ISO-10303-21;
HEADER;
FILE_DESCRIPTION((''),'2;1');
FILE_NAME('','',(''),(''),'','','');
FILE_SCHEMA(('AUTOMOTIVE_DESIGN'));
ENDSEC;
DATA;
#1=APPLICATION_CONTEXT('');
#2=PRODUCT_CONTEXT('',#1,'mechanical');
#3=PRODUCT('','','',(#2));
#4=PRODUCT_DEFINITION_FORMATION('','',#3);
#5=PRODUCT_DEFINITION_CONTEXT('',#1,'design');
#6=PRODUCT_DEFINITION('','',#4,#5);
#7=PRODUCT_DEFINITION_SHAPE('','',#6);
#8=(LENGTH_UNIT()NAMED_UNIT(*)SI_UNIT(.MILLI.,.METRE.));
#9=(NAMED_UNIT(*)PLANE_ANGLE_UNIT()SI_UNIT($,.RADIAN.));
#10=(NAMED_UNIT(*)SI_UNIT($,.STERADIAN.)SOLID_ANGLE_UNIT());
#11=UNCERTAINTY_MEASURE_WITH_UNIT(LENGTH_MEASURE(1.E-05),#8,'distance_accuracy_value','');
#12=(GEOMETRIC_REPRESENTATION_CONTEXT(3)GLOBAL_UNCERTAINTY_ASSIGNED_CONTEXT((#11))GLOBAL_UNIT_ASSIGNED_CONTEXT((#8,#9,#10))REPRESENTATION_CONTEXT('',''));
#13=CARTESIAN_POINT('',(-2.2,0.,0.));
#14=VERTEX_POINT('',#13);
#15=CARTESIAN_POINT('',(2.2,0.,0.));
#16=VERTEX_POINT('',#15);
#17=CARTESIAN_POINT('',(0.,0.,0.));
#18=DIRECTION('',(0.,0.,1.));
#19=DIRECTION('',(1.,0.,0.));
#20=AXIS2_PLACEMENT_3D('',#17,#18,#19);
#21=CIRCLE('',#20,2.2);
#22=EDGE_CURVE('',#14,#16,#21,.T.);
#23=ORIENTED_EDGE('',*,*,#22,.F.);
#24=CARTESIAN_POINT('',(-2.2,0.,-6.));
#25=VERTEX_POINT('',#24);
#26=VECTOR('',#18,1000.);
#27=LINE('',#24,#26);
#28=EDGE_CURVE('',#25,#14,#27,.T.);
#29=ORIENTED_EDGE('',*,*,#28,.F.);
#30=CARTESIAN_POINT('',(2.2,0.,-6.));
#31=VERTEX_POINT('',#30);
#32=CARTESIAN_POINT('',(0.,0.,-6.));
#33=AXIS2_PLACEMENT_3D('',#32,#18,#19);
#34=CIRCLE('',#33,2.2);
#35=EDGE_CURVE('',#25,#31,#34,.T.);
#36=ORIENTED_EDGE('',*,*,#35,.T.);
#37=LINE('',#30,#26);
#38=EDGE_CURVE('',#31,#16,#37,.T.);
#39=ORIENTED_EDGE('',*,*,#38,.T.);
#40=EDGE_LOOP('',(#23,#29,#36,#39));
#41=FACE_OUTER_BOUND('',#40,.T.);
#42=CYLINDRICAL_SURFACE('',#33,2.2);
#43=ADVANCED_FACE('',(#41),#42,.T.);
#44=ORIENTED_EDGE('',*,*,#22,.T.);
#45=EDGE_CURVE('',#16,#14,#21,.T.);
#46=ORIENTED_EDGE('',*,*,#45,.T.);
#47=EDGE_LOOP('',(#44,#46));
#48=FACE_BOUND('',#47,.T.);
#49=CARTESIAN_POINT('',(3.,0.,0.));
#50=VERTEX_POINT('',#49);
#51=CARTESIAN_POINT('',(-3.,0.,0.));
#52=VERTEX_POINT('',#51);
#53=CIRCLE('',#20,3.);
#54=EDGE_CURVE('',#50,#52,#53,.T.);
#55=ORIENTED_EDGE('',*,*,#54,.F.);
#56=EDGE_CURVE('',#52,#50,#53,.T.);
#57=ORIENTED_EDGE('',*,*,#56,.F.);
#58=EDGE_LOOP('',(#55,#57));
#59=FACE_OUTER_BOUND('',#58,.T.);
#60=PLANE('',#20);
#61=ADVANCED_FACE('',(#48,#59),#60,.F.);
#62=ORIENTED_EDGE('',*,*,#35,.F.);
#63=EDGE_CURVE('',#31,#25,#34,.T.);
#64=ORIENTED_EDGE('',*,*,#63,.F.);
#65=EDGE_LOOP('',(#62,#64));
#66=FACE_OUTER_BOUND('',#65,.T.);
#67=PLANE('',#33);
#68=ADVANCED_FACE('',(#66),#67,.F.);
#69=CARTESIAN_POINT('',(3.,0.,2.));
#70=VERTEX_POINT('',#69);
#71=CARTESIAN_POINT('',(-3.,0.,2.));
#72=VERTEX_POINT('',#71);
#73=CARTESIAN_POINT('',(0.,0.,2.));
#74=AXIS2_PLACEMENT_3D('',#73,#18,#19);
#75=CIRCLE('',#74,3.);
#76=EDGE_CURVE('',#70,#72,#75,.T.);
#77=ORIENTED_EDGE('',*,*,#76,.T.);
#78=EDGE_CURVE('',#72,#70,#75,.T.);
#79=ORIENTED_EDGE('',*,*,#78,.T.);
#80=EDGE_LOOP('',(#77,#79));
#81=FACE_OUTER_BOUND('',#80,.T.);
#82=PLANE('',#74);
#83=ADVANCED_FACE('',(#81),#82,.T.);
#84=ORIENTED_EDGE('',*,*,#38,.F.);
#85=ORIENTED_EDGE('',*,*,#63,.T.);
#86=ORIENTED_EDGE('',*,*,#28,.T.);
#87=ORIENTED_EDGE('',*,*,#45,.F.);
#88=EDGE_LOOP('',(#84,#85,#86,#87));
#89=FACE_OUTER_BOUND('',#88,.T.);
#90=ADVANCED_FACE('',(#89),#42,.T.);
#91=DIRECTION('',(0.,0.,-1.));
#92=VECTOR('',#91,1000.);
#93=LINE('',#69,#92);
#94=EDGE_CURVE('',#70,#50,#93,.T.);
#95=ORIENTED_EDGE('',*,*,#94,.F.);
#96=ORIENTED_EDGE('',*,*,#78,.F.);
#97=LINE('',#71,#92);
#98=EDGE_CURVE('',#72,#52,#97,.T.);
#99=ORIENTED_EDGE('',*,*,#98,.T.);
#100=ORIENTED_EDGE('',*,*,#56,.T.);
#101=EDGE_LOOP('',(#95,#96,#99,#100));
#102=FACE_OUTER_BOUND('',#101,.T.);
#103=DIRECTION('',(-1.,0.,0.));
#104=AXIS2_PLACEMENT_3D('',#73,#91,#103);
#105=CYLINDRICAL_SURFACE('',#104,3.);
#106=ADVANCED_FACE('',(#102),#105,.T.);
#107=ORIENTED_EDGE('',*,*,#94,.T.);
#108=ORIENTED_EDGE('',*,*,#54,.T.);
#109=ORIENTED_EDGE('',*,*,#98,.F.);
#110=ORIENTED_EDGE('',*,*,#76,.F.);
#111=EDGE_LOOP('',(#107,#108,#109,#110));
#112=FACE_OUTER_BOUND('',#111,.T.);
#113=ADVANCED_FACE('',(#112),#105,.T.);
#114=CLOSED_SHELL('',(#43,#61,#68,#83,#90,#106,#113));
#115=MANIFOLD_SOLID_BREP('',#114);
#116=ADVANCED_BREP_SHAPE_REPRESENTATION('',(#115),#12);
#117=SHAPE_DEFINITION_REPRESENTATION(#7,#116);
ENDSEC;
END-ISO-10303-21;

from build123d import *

# Parameters (mm, degrees)
SKETCH_1_R      = 2.2
EXTRUDE_1_DEPTH = 6
SKETCH_2_R      = 3
EXTRUDE_2_DEPTH = 2


with BuildPart() as part:
    # 草图1 → 凸台-拉伸1 (new body)
    with BuildSketch(Plane.XY):
        Circle(SKETCH_1_R)
    extrude(amount=-EXTRUDE_1_DEPTH)

    # 草图2 → 凸台-拉伸2 (add)
    with BuildSketch(Plane.XY):
        Circle(SKETCH_2_R)
    extrude(amount=EXTRUDE_2_DEPTH)


solid = part.part
